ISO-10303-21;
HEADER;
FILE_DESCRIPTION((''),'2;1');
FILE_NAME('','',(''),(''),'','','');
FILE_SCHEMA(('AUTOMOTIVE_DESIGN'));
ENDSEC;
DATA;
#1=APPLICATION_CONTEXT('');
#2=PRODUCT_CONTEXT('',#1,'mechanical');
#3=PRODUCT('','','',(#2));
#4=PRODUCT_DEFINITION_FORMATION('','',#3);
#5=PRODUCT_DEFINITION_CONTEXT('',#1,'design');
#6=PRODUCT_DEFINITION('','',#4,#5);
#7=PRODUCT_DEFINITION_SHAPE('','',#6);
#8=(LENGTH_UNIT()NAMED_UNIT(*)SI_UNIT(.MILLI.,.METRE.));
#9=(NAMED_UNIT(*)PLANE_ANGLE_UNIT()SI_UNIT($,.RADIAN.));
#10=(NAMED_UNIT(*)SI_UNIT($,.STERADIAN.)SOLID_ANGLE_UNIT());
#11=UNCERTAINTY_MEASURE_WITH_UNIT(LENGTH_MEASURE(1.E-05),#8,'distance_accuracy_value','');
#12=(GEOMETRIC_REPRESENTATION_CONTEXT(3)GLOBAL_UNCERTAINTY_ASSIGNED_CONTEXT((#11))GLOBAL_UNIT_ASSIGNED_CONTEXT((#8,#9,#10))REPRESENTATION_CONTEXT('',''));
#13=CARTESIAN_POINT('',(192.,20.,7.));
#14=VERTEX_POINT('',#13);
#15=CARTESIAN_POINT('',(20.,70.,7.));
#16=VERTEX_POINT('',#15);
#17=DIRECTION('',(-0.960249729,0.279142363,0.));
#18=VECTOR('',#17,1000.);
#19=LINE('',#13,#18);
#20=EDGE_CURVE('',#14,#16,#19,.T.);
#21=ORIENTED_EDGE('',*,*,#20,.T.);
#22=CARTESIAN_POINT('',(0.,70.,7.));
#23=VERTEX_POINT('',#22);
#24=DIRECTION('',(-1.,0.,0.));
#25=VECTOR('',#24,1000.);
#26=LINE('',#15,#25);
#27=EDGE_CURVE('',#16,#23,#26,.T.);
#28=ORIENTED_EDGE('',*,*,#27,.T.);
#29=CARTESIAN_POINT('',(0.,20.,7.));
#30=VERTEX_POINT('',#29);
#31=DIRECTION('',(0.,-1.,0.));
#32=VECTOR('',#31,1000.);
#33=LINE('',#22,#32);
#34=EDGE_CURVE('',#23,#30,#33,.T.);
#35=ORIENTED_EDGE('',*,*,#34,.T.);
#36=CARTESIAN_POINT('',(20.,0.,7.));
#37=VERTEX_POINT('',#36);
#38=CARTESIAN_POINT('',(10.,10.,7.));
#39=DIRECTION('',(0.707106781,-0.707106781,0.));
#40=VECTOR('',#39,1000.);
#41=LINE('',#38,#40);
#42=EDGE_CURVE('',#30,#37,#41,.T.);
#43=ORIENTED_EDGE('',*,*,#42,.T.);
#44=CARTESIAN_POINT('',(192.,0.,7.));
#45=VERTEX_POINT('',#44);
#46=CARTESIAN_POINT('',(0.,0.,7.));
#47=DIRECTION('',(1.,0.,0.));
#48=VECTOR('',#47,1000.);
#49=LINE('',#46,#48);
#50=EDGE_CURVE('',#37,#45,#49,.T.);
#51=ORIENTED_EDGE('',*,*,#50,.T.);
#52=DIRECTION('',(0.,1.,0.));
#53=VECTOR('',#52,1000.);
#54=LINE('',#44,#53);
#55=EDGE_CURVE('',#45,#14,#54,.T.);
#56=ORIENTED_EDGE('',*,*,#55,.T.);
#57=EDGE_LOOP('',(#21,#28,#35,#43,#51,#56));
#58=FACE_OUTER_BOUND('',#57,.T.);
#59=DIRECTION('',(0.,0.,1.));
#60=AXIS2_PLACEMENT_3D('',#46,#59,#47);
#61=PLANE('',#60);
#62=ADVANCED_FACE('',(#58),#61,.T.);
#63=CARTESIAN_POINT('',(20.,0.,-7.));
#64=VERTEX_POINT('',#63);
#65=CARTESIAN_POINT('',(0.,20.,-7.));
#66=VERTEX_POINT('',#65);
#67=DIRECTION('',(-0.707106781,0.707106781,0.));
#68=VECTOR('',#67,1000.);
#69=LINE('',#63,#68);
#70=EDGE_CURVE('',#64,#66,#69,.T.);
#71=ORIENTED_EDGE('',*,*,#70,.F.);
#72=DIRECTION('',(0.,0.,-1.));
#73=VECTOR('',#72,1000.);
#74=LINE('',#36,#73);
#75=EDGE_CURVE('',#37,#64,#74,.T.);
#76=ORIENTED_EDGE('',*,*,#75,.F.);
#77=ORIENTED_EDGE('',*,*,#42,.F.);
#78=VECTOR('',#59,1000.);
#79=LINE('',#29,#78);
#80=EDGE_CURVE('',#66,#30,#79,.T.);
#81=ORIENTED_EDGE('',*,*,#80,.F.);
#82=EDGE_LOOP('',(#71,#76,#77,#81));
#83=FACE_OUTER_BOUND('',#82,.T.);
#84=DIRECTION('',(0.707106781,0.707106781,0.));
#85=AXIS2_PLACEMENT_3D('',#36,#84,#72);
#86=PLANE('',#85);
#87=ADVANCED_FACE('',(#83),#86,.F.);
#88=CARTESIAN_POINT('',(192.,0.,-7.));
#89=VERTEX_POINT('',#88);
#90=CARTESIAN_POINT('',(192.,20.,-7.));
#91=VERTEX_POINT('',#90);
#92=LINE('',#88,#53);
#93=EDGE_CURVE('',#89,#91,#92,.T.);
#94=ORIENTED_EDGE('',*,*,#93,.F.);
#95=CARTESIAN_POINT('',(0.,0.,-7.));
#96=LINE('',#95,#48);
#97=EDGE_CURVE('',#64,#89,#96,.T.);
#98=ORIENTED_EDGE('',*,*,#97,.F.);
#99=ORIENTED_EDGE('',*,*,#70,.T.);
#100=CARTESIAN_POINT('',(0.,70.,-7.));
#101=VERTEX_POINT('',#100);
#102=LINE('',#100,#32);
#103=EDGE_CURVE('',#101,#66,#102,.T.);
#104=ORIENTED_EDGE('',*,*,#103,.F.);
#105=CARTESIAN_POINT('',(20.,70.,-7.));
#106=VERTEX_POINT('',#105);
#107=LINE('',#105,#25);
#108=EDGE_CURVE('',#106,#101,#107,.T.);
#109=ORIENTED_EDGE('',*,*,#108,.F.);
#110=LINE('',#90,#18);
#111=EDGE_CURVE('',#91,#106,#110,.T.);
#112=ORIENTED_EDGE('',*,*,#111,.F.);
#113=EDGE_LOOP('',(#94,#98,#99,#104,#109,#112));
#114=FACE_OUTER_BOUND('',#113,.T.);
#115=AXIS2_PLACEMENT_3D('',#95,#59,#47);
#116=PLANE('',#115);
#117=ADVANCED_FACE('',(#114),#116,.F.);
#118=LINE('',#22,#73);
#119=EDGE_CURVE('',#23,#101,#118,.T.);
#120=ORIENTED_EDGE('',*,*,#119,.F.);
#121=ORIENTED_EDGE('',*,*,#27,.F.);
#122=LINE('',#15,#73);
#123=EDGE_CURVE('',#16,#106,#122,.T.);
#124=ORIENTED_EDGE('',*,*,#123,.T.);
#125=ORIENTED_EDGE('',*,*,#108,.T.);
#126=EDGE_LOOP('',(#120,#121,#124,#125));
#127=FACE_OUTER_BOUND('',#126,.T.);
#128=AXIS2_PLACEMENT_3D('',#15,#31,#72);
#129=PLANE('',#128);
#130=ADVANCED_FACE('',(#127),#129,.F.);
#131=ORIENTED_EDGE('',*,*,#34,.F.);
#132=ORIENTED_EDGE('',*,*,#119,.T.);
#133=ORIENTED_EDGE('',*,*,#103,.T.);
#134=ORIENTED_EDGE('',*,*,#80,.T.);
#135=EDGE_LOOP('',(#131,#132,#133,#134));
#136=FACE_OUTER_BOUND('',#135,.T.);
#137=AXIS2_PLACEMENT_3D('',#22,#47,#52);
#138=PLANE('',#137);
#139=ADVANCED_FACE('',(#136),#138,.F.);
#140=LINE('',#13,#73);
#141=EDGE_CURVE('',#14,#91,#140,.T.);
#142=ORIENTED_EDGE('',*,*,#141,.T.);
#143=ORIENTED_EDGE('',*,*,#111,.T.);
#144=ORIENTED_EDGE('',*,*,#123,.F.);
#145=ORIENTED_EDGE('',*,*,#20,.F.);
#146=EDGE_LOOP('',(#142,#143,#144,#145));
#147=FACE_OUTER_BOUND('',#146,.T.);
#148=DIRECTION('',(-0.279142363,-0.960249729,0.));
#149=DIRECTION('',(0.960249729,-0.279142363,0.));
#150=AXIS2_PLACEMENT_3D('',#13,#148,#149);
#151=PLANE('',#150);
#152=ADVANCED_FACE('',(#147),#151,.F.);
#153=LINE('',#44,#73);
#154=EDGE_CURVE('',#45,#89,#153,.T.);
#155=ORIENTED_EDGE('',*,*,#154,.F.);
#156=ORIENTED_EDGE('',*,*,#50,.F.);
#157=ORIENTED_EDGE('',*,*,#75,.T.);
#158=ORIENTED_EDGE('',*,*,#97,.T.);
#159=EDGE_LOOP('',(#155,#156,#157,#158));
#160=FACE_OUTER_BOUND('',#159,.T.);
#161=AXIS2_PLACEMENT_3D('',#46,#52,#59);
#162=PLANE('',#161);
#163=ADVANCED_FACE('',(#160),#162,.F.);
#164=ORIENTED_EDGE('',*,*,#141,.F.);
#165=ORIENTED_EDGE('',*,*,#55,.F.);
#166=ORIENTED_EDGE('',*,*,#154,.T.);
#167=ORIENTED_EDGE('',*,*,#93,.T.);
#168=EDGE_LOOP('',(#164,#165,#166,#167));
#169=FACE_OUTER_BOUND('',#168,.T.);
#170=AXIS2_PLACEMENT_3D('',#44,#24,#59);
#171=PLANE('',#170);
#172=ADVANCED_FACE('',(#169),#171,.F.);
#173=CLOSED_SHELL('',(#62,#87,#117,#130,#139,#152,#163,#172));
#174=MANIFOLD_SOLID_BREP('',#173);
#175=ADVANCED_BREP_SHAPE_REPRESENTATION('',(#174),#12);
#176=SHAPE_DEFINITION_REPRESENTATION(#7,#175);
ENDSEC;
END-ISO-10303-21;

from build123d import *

# Parameters (mm, degrees)
BOSS_EXTRUDE1_DEPTH = 7
CHAMFER1_SIZE       = 20


with BuildPart() as part:
    # Sketch1 → Boss-Extrude1 (new, symmetric)
    with BuildSketch(Plane.XY):
        Polygon((0, 0), (192, 0), (192, 20), (20, 70), (0, 70), align=None)
    extrude(amount=BOSS_EXTRUDE1_DEPTH, both=True)

    # Chamfer1
    chamfer1_edges = [part.edges().sort_by_distance(p)[0] for p in [
        (0, 0, 0),
    ]]
    chamfer(chamfer1_edges, length=CHAMFER1_SIZE)


solid = part.part
